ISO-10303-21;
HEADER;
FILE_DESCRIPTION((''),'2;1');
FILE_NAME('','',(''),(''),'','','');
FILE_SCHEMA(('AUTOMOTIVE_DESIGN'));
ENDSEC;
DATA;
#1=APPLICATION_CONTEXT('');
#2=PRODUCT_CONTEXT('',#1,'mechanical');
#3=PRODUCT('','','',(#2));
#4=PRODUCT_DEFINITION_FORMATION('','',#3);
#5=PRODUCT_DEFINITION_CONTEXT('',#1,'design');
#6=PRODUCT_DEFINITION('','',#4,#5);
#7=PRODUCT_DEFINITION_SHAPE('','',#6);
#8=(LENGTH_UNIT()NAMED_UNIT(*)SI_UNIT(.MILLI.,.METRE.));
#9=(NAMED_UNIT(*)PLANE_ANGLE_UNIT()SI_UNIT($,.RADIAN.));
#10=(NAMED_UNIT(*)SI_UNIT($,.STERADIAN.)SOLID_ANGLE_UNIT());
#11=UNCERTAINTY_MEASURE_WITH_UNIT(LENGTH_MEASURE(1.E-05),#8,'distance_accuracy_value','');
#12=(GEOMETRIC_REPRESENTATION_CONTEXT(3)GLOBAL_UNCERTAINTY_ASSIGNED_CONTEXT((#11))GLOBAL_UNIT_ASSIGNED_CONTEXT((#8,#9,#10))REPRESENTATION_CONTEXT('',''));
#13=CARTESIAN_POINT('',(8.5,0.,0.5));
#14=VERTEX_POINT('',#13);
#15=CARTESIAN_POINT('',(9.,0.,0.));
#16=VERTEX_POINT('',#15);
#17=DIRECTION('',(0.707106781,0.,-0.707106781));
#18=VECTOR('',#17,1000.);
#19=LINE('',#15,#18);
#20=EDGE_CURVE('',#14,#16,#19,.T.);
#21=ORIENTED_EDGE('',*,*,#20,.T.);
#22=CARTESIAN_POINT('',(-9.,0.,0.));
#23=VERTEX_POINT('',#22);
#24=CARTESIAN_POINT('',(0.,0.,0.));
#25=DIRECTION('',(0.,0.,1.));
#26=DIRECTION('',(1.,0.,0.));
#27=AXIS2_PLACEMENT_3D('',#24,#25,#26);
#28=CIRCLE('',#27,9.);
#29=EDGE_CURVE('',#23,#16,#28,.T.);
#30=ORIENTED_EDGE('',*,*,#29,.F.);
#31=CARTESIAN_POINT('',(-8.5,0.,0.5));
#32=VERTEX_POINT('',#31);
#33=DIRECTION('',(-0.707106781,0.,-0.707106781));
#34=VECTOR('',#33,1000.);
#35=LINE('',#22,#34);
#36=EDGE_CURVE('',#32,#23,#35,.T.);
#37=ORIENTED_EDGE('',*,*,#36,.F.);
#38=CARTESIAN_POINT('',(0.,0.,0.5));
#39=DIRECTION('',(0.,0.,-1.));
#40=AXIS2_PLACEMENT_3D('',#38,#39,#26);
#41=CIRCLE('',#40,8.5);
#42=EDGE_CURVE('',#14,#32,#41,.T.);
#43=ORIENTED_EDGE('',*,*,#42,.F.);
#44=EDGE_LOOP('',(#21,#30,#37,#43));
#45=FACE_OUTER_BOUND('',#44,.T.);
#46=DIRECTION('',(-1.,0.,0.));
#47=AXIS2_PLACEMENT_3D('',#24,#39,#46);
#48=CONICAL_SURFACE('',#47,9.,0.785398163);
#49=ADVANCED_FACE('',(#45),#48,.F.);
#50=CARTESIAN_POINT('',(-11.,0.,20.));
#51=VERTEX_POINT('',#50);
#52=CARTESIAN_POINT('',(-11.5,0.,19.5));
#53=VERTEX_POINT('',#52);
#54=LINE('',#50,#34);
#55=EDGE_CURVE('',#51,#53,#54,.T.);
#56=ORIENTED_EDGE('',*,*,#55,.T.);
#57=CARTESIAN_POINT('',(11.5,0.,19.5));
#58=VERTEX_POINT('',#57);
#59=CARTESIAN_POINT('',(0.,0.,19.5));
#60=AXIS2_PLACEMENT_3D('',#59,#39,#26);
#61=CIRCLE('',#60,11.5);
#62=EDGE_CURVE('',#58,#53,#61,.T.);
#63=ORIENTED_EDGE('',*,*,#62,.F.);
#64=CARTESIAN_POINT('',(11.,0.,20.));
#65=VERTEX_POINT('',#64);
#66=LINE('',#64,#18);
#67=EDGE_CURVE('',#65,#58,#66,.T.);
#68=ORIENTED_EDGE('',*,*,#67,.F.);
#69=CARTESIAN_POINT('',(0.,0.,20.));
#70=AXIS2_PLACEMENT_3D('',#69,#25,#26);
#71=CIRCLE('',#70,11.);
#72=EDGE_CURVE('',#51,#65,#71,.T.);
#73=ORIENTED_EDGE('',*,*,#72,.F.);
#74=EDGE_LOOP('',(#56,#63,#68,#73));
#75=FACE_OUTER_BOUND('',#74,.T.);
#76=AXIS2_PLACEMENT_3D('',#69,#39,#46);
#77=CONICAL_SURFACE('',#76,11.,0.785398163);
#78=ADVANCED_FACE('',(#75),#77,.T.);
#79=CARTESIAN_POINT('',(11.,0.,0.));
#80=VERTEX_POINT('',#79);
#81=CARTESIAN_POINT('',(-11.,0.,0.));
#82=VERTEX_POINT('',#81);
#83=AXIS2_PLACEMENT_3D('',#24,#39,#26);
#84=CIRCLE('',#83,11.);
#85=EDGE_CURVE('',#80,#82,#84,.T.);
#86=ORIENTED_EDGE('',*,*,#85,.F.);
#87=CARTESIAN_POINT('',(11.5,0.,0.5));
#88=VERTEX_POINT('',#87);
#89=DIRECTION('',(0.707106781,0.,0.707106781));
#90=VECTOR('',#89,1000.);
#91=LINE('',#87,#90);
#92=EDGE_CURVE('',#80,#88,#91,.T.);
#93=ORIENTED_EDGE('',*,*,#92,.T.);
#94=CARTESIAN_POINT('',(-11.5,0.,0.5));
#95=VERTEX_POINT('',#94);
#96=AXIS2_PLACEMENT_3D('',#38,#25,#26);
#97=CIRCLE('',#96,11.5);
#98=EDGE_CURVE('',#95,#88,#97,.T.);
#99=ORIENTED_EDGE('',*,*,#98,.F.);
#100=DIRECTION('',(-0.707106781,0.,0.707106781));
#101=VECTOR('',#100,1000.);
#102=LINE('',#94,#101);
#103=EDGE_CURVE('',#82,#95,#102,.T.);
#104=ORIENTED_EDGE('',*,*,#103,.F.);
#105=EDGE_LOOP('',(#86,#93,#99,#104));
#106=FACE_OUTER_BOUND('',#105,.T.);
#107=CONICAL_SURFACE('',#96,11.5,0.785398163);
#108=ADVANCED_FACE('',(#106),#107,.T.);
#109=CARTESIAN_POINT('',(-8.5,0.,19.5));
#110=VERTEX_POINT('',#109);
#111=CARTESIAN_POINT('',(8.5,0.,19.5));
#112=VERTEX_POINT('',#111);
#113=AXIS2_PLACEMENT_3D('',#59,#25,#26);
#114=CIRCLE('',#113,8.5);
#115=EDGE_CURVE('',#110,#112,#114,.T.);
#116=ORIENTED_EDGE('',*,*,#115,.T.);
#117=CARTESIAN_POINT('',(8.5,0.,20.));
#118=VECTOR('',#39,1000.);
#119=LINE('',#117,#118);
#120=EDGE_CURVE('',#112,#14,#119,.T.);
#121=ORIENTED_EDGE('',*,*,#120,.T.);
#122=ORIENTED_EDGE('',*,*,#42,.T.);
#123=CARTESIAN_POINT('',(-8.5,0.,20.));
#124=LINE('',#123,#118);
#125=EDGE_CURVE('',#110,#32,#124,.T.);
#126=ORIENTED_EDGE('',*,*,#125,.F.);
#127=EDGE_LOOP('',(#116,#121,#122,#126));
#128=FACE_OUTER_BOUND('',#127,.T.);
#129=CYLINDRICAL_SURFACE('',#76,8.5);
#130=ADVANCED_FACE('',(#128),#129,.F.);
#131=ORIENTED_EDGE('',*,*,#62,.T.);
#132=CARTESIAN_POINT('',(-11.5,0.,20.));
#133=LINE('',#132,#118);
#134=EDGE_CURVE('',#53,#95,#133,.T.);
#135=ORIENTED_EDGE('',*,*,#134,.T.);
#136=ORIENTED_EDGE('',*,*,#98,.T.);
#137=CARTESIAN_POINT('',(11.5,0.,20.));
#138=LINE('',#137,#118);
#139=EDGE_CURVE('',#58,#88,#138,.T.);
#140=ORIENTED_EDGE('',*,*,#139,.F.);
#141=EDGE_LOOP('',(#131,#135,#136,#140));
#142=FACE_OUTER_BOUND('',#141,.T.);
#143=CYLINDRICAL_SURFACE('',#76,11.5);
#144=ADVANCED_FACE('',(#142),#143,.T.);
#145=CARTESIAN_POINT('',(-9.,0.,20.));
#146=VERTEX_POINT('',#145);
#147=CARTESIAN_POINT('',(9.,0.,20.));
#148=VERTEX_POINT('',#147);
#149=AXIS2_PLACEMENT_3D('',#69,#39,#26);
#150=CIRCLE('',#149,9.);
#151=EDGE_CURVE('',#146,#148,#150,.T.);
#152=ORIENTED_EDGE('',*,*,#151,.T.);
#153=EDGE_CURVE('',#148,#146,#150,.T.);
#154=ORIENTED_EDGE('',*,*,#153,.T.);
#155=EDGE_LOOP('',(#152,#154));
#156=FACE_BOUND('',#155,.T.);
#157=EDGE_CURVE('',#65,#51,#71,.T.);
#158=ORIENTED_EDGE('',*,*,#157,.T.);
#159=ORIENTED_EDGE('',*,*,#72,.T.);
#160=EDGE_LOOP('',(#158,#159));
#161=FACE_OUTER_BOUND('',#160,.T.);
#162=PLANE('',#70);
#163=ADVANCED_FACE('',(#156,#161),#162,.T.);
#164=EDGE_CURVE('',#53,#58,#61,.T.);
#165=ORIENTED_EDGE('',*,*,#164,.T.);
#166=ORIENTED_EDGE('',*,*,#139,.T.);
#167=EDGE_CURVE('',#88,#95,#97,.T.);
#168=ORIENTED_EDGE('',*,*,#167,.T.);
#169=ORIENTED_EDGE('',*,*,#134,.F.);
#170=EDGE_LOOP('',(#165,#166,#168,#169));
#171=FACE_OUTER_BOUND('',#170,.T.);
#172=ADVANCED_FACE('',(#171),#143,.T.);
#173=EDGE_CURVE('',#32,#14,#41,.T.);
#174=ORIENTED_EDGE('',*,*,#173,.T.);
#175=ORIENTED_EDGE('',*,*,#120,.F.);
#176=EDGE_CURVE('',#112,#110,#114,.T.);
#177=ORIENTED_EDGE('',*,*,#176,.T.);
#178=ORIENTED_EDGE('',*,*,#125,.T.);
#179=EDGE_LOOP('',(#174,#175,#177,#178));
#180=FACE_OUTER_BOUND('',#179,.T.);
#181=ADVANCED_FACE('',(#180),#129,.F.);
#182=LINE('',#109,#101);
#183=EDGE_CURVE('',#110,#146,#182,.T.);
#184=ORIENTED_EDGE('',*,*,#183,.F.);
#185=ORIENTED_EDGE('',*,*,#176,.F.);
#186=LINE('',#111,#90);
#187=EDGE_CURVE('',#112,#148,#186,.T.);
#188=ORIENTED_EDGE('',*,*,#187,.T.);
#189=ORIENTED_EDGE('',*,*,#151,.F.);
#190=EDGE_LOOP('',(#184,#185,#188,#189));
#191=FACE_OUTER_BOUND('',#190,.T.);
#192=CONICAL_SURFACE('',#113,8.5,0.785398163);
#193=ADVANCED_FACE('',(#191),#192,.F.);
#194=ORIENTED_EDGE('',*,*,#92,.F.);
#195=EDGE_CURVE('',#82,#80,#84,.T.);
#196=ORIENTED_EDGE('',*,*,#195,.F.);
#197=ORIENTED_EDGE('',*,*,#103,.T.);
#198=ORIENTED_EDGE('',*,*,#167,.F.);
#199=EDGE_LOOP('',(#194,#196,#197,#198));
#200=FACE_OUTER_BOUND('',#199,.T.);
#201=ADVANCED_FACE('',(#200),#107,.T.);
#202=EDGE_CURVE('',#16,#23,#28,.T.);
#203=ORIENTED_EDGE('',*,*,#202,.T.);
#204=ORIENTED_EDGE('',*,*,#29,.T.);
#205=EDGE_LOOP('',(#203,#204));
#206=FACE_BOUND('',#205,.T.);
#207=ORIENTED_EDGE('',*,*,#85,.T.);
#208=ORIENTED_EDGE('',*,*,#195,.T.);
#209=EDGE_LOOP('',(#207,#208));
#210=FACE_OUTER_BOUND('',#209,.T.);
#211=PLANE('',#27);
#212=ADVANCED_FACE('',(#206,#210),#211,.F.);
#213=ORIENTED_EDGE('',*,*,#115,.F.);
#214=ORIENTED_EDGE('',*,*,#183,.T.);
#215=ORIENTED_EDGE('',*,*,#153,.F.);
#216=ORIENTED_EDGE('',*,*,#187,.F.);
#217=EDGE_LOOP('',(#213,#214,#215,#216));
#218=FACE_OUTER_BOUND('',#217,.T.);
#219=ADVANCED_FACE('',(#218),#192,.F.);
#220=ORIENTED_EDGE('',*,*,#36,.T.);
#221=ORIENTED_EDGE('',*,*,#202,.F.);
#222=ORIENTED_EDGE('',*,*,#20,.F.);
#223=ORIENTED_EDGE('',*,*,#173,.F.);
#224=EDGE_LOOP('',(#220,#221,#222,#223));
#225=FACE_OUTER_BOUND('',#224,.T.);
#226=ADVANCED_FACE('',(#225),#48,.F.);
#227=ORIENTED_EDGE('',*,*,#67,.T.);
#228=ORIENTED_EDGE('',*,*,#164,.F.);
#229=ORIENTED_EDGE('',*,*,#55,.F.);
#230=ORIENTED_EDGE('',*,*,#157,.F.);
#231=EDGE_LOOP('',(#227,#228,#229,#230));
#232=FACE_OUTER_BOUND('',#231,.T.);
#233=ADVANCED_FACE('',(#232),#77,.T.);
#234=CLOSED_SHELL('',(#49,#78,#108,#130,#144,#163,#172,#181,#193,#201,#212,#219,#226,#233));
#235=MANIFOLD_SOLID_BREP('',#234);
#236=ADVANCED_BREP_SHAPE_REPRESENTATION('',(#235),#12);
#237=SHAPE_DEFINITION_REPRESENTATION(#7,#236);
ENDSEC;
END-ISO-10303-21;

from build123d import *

# Parameters (mm, degrees)
SKETCH1_R           = 11.5
SKETCH1_R_2         = 8.5
BOSS_EXTRUDE1_DEPTH = 20
CHAMFER1_SIZE       = 0.5


with BuildPart() as part:
    # Sketch1 → Boss-Extrude1 (new body)
    with BuildSketch(Plane.XY):
        Circle(SKETCH1_R)
        Circle(SKETCH1_R_2, mode=Mode.SUBTRACT)
    extrude(amount=BOSS_EXTRUDE1_DEPTH)

    # Chamfer1
    chamfer1_edges = [part.edges().sort_by_distance(p)[0] for p in [
        (-11.5, 0, 0),
        (-11.5, 0, 20),
        (-8.5, 0, 0),
        (-8.5, 0, 20),
    ]]
    chamfer(chamfer1_edges, length=CHAMFER1_SIZE)


solid = part.part
